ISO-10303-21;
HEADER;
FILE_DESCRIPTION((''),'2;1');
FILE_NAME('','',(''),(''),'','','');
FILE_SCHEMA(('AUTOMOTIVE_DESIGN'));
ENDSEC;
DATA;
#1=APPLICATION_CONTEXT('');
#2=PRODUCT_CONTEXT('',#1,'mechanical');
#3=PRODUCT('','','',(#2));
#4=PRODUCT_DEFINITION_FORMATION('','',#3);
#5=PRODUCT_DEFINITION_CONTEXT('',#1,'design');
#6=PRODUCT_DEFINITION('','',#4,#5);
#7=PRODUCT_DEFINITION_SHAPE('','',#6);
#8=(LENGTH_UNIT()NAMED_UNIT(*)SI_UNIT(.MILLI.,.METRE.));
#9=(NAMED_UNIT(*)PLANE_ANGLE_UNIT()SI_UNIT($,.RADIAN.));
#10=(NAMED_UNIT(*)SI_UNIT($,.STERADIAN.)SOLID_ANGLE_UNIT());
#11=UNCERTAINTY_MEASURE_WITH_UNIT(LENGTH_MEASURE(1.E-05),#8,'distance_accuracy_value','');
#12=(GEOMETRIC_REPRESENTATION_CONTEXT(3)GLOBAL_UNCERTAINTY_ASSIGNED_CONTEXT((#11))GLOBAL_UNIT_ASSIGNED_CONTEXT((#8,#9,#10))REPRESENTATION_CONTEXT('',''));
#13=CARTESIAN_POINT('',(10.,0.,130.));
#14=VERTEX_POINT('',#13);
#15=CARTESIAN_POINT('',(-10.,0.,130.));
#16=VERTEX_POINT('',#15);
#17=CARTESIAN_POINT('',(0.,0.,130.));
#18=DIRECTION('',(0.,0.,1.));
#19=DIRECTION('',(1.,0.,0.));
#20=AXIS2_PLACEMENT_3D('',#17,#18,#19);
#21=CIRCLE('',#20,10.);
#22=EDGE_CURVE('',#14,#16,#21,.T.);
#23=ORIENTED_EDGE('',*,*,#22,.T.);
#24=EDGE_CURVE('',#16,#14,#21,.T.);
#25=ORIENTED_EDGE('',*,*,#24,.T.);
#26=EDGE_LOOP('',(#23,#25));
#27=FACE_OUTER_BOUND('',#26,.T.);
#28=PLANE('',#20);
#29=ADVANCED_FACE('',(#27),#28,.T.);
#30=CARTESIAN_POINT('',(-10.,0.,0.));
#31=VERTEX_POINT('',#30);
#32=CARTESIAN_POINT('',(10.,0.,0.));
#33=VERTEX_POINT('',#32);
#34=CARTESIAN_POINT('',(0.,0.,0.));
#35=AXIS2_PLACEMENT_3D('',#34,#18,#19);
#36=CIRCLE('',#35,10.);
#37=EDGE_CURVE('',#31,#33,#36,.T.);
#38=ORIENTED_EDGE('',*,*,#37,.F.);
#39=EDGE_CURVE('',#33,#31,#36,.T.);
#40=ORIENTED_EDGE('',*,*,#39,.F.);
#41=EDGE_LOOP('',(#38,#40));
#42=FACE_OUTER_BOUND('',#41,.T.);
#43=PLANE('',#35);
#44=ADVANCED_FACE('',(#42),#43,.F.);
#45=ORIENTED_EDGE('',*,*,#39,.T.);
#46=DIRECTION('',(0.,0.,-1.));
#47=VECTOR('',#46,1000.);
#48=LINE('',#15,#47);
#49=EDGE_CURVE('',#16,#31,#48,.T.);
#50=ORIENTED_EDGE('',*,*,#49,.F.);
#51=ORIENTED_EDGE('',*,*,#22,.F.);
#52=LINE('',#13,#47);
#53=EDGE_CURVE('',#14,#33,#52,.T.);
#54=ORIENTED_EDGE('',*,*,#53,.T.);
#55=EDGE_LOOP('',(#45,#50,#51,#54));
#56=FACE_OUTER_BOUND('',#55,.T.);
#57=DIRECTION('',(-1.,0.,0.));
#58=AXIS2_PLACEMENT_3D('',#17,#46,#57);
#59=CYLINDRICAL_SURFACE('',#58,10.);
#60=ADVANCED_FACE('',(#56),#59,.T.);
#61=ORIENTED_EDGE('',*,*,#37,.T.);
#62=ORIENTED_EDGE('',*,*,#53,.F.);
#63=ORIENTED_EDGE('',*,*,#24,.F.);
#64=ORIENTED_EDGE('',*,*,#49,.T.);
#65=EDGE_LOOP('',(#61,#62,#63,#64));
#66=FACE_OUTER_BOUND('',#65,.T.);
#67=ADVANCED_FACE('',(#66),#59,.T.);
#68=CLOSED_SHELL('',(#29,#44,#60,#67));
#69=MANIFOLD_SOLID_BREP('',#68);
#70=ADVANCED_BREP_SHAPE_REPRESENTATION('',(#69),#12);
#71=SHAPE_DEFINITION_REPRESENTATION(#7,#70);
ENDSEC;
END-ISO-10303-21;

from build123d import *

# Parameters (mm, degrees)
SKETCH_1_R      = 10
EXTRUDE_1_DEPTH = 130


with BuildPart() as part:
    # 草图1 → 凸台-拉伸1 (new body)
    with BuildSketch(Plane.XY):
        Circle(SKETCH_1_R)
    extrude(amount=EXTRUDE_1_DEPTH)


solid = part.part
